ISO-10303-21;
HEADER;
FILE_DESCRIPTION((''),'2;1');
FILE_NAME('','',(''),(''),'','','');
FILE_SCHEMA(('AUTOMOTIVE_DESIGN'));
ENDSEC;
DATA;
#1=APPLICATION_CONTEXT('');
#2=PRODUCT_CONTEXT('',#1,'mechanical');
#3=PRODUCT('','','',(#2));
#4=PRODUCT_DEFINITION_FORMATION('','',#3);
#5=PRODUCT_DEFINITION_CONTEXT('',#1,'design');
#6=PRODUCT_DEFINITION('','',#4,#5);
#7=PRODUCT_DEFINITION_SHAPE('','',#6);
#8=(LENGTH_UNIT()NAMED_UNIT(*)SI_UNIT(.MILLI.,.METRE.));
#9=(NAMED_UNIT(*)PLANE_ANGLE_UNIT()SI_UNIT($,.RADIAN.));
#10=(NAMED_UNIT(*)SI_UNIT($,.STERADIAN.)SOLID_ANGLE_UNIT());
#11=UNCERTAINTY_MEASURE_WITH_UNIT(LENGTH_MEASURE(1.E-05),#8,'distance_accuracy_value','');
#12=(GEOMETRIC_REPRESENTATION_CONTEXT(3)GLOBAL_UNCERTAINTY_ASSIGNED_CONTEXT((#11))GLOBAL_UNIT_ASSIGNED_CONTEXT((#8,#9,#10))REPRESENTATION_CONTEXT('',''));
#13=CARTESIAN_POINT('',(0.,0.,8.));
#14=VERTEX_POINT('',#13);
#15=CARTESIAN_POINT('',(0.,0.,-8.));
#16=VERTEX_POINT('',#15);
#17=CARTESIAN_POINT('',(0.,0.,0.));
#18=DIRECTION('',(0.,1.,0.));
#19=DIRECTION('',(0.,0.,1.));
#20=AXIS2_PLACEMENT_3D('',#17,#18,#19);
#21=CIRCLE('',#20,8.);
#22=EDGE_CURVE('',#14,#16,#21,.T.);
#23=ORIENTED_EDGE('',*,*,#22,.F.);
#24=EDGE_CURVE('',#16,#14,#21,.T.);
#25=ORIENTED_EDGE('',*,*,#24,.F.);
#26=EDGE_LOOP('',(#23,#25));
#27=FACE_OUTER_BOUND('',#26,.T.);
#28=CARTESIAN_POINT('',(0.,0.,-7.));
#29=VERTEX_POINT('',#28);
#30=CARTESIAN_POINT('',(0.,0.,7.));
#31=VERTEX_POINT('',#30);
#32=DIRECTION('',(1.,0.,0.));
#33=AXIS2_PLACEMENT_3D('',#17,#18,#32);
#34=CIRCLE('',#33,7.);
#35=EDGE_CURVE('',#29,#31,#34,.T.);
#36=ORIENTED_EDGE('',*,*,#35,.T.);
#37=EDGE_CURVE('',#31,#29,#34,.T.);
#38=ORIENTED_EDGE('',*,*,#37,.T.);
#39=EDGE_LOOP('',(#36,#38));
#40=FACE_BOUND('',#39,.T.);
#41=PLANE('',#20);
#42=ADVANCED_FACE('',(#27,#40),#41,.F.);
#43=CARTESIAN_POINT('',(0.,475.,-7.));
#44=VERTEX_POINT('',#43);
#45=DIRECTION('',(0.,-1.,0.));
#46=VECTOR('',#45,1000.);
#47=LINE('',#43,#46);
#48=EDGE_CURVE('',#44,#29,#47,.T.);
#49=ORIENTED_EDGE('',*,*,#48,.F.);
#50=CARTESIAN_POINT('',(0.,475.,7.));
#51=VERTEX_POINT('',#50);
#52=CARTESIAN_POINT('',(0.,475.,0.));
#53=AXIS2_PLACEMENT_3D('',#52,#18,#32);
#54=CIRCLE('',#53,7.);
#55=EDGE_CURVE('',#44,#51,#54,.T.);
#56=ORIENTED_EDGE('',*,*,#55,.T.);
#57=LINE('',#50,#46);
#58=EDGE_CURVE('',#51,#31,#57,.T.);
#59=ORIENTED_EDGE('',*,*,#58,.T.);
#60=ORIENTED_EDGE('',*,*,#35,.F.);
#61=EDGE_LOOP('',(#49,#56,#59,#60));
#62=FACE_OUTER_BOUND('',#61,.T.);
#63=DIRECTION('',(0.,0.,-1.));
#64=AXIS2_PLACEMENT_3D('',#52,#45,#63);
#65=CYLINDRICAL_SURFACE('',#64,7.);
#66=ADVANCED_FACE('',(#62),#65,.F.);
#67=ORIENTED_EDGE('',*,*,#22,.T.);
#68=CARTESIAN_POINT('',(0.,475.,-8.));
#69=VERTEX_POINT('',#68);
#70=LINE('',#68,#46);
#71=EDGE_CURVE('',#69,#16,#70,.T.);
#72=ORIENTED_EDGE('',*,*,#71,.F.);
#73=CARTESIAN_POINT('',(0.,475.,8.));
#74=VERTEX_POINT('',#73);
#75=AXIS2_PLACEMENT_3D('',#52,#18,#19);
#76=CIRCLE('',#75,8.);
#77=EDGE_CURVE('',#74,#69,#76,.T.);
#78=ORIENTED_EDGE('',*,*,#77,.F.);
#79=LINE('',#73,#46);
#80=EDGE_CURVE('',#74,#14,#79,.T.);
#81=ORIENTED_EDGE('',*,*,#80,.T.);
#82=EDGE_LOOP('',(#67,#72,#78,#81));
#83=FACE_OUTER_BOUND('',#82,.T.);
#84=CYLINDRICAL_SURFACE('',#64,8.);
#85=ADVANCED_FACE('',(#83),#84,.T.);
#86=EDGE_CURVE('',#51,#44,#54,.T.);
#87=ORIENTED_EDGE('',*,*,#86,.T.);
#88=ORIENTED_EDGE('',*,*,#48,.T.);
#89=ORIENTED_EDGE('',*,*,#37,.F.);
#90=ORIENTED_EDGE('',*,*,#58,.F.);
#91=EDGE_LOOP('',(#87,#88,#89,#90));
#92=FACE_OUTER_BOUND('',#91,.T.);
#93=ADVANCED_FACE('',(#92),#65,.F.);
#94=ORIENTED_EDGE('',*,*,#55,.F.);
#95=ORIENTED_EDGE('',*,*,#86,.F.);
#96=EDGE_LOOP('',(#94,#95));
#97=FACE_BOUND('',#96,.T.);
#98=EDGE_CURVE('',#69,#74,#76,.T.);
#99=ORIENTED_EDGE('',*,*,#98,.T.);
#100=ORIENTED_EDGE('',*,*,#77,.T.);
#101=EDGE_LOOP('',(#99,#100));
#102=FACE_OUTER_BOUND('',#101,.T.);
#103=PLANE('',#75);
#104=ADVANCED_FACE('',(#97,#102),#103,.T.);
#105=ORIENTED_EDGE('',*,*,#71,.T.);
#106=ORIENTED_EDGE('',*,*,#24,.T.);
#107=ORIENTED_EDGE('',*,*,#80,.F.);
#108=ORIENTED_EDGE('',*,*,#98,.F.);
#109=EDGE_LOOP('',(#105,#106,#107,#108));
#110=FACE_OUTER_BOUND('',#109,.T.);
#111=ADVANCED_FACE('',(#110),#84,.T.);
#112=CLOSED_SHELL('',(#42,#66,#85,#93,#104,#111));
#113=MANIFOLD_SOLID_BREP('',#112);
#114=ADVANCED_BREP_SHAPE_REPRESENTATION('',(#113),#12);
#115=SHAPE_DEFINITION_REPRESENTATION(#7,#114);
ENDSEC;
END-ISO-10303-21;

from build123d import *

# Parameters (mm, degrees)
SKETCH_1_R      = 8
SKETCH_1_R_2    = 7
EXTRUDE_1_DEPTH = 475


with BuildPart() as part:
    # 草图1 → 拉伸-薄壁1 (new body)
    with BuildSketch(Plane(origin=(0, 0, 0), x_dir=(1, 0, 0), z_dir=(0, 1, 0))):
        Circle(SKETCH_1_R)
        Circle(SKETCH_1_R_2, mode=Mode.SUBTRACT)
    extrude(amount=EXTRUDE_1_DEPTH)


solid = part.part
